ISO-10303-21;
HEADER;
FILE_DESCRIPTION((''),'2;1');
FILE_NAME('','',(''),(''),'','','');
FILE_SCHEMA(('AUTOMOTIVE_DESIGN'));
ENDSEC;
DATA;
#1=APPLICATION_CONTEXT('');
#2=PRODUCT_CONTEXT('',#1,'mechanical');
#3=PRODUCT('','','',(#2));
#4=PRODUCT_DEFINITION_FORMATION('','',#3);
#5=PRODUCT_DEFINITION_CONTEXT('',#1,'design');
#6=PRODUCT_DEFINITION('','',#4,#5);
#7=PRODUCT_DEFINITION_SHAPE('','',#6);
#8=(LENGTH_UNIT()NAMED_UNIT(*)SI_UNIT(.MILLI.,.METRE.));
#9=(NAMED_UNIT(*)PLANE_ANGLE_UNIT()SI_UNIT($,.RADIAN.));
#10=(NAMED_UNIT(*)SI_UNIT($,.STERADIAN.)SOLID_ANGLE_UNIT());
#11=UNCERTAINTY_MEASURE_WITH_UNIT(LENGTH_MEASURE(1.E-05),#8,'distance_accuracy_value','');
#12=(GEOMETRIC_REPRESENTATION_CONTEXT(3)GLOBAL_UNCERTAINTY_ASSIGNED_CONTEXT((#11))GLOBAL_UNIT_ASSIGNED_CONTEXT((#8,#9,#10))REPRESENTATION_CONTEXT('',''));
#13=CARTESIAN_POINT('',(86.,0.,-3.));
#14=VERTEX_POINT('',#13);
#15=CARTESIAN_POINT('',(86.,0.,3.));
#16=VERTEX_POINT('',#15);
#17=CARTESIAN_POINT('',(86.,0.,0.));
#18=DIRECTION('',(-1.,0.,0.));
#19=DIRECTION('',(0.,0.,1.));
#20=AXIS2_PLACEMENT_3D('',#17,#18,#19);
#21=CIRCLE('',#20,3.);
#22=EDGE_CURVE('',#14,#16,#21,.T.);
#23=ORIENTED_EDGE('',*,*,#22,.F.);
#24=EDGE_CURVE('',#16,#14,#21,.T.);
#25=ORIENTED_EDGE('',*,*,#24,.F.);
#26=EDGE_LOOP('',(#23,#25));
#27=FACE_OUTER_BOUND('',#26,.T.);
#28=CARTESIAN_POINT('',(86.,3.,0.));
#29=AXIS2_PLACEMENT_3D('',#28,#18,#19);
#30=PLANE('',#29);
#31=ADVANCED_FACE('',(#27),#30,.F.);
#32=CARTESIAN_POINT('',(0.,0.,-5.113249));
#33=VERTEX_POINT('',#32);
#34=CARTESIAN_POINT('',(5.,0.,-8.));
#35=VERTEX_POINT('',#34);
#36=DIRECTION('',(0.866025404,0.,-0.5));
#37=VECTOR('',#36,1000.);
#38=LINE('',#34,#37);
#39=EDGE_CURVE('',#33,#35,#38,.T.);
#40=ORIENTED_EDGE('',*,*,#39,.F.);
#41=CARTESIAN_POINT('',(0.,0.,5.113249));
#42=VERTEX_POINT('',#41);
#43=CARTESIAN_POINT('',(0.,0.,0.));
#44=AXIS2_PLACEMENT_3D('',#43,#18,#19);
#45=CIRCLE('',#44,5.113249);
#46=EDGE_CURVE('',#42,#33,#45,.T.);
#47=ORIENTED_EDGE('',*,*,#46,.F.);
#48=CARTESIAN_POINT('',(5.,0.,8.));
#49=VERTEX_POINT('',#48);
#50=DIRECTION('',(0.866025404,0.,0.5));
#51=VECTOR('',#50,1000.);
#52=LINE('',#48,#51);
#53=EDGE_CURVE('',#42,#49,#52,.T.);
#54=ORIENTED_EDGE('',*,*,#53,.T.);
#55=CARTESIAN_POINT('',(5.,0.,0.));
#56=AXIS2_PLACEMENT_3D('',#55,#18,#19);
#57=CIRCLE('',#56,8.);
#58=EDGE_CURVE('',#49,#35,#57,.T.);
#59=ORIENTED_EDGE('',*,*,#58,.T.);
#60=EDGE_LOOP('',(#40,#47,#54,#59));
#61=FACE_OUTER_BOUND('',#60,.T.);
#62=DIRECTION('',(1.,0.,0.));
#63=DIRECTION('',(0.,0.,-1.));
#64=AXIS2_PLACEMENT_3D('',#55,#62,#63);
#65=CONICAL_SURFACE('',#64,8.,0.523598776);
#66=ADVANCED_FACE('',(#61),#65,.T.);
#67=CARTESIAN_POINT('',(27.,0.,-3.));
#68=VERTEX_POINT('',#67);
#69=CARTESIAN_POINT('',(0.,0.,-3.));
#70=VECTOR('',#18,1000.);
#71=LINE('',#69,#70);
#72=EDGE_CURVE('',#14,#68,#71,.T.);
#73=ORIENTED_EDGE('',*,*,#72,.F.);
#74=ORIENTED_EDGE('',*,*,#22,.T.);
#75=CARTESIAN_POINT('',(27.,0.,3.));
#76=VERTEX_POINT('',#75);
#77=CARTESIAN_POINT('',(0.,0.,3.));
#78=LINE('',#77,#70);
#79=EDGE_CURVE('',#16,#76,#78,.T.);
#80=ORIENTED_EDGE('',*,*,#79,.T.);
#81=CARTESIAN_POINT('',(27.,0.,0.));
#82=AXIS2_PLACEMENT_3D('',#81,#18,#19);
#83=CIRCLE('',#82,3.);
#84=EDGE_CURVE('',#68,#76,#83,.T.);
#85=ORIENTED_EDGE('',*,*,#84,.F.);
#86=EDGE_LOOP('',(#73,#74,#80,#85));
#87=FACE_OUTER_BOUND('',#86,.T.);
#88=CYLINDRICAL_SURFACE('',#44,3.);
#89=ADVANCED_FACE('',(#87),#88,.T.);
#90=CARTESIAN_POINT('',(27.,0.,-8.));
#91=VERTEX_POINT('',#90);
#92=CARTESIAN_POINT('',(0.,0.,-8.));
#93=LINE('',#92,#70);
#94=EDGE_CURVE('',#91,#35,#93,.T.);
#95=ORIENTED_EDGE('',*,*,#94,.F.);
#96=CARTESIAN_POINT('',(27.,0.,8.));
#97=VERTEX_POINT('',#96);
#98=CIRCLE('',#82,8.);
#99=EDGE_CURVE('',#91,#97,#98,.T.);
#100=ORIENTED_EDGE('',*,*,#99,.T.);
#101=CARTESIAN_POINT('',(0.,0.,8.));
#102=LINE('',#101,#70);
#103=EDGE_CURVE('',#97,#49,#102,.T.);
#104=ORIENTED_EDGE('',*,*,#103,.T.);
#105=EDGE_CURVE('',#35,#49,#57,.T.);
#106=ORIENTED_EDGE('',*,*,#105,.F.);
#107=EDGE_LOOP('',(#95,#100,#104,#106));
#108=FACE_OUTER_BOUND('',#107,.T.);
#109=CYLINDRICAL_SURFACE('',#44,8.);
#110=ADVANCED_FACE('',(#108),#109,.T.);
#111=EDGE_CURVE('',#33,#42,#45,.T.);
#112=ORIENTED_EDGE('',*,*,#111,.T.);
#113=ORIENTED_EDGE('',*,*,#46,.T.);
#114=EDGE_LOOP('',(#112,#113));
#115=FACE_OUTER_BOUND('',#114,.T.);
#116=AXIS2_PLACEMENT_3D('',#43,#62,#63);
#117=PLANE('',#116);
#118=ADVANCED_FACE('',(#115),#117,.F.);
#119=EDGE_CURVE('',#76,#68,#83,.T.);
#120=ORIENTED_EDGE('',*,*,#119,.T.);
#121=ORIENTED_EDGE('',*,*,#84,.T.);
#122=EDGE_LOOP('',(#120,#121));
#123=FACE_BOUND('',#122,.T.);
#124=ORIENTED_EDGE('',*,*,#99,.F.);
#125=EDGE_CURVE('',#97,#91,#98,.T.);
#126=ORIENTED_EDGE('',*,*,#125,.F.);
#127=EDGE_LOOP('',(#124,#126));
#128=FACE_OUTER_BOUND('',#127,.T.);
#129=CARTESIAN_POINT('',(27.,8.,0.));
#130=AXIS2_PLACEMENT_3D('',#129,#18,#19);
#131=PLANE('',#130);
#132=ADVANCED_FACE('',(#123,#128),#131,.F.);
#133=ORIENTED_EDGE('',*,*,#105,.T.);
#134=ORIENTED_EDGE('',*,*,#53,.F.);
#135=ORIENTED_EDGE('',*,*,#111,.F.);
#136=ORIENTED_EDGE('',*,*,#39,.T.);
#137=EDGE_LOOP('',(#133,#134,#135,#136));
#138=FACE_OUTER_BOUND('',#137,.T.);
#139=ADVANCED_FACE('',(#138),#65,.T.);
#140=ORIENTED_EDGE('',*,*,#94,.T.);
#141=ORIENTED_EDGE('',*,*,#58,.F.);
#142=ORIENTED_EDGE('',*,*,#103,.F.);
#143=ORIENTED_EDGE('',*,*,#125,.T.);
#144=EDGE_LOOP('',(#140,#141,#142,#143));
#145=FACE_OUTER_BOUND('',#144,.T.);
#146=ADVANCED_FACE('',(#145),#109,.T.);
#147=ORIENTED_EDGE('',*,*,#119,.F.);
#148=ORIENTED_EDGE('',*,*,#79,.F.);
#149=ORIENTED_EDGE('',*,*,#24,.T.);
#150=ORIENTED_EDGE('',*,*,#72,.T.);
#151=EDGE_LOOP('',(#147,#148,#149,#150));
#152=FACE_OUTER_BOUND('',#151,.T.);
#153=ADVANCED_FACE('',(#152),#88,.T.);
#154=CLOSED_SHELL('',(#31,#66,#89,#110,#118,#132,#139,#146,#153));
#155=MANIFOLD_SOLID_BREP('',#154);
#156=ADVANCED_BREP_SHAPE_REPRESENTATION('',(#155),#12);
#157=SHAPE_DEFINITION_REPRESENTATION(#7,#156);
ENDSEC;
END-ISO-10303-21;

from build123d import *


with BuildPart() as part:
    # Sketch1 → Revolve1 (revolve)
    with BuildSketch(Plane.XY, mode=Mode.PRIVATE) as revolve1_sk:
        Polygon((0, 0), (0, 5.113248654), (5, 8), (27, 8), (27, 3), (86, 3), (86, 0), align=None)
    revolve(revolve1_sk.sketch.rotate(Axis((0, 0, 0), (1, 0, 0)), 90), axis=Axis((0, 0, 0), (1, 0, 0)))


solid = part.part
